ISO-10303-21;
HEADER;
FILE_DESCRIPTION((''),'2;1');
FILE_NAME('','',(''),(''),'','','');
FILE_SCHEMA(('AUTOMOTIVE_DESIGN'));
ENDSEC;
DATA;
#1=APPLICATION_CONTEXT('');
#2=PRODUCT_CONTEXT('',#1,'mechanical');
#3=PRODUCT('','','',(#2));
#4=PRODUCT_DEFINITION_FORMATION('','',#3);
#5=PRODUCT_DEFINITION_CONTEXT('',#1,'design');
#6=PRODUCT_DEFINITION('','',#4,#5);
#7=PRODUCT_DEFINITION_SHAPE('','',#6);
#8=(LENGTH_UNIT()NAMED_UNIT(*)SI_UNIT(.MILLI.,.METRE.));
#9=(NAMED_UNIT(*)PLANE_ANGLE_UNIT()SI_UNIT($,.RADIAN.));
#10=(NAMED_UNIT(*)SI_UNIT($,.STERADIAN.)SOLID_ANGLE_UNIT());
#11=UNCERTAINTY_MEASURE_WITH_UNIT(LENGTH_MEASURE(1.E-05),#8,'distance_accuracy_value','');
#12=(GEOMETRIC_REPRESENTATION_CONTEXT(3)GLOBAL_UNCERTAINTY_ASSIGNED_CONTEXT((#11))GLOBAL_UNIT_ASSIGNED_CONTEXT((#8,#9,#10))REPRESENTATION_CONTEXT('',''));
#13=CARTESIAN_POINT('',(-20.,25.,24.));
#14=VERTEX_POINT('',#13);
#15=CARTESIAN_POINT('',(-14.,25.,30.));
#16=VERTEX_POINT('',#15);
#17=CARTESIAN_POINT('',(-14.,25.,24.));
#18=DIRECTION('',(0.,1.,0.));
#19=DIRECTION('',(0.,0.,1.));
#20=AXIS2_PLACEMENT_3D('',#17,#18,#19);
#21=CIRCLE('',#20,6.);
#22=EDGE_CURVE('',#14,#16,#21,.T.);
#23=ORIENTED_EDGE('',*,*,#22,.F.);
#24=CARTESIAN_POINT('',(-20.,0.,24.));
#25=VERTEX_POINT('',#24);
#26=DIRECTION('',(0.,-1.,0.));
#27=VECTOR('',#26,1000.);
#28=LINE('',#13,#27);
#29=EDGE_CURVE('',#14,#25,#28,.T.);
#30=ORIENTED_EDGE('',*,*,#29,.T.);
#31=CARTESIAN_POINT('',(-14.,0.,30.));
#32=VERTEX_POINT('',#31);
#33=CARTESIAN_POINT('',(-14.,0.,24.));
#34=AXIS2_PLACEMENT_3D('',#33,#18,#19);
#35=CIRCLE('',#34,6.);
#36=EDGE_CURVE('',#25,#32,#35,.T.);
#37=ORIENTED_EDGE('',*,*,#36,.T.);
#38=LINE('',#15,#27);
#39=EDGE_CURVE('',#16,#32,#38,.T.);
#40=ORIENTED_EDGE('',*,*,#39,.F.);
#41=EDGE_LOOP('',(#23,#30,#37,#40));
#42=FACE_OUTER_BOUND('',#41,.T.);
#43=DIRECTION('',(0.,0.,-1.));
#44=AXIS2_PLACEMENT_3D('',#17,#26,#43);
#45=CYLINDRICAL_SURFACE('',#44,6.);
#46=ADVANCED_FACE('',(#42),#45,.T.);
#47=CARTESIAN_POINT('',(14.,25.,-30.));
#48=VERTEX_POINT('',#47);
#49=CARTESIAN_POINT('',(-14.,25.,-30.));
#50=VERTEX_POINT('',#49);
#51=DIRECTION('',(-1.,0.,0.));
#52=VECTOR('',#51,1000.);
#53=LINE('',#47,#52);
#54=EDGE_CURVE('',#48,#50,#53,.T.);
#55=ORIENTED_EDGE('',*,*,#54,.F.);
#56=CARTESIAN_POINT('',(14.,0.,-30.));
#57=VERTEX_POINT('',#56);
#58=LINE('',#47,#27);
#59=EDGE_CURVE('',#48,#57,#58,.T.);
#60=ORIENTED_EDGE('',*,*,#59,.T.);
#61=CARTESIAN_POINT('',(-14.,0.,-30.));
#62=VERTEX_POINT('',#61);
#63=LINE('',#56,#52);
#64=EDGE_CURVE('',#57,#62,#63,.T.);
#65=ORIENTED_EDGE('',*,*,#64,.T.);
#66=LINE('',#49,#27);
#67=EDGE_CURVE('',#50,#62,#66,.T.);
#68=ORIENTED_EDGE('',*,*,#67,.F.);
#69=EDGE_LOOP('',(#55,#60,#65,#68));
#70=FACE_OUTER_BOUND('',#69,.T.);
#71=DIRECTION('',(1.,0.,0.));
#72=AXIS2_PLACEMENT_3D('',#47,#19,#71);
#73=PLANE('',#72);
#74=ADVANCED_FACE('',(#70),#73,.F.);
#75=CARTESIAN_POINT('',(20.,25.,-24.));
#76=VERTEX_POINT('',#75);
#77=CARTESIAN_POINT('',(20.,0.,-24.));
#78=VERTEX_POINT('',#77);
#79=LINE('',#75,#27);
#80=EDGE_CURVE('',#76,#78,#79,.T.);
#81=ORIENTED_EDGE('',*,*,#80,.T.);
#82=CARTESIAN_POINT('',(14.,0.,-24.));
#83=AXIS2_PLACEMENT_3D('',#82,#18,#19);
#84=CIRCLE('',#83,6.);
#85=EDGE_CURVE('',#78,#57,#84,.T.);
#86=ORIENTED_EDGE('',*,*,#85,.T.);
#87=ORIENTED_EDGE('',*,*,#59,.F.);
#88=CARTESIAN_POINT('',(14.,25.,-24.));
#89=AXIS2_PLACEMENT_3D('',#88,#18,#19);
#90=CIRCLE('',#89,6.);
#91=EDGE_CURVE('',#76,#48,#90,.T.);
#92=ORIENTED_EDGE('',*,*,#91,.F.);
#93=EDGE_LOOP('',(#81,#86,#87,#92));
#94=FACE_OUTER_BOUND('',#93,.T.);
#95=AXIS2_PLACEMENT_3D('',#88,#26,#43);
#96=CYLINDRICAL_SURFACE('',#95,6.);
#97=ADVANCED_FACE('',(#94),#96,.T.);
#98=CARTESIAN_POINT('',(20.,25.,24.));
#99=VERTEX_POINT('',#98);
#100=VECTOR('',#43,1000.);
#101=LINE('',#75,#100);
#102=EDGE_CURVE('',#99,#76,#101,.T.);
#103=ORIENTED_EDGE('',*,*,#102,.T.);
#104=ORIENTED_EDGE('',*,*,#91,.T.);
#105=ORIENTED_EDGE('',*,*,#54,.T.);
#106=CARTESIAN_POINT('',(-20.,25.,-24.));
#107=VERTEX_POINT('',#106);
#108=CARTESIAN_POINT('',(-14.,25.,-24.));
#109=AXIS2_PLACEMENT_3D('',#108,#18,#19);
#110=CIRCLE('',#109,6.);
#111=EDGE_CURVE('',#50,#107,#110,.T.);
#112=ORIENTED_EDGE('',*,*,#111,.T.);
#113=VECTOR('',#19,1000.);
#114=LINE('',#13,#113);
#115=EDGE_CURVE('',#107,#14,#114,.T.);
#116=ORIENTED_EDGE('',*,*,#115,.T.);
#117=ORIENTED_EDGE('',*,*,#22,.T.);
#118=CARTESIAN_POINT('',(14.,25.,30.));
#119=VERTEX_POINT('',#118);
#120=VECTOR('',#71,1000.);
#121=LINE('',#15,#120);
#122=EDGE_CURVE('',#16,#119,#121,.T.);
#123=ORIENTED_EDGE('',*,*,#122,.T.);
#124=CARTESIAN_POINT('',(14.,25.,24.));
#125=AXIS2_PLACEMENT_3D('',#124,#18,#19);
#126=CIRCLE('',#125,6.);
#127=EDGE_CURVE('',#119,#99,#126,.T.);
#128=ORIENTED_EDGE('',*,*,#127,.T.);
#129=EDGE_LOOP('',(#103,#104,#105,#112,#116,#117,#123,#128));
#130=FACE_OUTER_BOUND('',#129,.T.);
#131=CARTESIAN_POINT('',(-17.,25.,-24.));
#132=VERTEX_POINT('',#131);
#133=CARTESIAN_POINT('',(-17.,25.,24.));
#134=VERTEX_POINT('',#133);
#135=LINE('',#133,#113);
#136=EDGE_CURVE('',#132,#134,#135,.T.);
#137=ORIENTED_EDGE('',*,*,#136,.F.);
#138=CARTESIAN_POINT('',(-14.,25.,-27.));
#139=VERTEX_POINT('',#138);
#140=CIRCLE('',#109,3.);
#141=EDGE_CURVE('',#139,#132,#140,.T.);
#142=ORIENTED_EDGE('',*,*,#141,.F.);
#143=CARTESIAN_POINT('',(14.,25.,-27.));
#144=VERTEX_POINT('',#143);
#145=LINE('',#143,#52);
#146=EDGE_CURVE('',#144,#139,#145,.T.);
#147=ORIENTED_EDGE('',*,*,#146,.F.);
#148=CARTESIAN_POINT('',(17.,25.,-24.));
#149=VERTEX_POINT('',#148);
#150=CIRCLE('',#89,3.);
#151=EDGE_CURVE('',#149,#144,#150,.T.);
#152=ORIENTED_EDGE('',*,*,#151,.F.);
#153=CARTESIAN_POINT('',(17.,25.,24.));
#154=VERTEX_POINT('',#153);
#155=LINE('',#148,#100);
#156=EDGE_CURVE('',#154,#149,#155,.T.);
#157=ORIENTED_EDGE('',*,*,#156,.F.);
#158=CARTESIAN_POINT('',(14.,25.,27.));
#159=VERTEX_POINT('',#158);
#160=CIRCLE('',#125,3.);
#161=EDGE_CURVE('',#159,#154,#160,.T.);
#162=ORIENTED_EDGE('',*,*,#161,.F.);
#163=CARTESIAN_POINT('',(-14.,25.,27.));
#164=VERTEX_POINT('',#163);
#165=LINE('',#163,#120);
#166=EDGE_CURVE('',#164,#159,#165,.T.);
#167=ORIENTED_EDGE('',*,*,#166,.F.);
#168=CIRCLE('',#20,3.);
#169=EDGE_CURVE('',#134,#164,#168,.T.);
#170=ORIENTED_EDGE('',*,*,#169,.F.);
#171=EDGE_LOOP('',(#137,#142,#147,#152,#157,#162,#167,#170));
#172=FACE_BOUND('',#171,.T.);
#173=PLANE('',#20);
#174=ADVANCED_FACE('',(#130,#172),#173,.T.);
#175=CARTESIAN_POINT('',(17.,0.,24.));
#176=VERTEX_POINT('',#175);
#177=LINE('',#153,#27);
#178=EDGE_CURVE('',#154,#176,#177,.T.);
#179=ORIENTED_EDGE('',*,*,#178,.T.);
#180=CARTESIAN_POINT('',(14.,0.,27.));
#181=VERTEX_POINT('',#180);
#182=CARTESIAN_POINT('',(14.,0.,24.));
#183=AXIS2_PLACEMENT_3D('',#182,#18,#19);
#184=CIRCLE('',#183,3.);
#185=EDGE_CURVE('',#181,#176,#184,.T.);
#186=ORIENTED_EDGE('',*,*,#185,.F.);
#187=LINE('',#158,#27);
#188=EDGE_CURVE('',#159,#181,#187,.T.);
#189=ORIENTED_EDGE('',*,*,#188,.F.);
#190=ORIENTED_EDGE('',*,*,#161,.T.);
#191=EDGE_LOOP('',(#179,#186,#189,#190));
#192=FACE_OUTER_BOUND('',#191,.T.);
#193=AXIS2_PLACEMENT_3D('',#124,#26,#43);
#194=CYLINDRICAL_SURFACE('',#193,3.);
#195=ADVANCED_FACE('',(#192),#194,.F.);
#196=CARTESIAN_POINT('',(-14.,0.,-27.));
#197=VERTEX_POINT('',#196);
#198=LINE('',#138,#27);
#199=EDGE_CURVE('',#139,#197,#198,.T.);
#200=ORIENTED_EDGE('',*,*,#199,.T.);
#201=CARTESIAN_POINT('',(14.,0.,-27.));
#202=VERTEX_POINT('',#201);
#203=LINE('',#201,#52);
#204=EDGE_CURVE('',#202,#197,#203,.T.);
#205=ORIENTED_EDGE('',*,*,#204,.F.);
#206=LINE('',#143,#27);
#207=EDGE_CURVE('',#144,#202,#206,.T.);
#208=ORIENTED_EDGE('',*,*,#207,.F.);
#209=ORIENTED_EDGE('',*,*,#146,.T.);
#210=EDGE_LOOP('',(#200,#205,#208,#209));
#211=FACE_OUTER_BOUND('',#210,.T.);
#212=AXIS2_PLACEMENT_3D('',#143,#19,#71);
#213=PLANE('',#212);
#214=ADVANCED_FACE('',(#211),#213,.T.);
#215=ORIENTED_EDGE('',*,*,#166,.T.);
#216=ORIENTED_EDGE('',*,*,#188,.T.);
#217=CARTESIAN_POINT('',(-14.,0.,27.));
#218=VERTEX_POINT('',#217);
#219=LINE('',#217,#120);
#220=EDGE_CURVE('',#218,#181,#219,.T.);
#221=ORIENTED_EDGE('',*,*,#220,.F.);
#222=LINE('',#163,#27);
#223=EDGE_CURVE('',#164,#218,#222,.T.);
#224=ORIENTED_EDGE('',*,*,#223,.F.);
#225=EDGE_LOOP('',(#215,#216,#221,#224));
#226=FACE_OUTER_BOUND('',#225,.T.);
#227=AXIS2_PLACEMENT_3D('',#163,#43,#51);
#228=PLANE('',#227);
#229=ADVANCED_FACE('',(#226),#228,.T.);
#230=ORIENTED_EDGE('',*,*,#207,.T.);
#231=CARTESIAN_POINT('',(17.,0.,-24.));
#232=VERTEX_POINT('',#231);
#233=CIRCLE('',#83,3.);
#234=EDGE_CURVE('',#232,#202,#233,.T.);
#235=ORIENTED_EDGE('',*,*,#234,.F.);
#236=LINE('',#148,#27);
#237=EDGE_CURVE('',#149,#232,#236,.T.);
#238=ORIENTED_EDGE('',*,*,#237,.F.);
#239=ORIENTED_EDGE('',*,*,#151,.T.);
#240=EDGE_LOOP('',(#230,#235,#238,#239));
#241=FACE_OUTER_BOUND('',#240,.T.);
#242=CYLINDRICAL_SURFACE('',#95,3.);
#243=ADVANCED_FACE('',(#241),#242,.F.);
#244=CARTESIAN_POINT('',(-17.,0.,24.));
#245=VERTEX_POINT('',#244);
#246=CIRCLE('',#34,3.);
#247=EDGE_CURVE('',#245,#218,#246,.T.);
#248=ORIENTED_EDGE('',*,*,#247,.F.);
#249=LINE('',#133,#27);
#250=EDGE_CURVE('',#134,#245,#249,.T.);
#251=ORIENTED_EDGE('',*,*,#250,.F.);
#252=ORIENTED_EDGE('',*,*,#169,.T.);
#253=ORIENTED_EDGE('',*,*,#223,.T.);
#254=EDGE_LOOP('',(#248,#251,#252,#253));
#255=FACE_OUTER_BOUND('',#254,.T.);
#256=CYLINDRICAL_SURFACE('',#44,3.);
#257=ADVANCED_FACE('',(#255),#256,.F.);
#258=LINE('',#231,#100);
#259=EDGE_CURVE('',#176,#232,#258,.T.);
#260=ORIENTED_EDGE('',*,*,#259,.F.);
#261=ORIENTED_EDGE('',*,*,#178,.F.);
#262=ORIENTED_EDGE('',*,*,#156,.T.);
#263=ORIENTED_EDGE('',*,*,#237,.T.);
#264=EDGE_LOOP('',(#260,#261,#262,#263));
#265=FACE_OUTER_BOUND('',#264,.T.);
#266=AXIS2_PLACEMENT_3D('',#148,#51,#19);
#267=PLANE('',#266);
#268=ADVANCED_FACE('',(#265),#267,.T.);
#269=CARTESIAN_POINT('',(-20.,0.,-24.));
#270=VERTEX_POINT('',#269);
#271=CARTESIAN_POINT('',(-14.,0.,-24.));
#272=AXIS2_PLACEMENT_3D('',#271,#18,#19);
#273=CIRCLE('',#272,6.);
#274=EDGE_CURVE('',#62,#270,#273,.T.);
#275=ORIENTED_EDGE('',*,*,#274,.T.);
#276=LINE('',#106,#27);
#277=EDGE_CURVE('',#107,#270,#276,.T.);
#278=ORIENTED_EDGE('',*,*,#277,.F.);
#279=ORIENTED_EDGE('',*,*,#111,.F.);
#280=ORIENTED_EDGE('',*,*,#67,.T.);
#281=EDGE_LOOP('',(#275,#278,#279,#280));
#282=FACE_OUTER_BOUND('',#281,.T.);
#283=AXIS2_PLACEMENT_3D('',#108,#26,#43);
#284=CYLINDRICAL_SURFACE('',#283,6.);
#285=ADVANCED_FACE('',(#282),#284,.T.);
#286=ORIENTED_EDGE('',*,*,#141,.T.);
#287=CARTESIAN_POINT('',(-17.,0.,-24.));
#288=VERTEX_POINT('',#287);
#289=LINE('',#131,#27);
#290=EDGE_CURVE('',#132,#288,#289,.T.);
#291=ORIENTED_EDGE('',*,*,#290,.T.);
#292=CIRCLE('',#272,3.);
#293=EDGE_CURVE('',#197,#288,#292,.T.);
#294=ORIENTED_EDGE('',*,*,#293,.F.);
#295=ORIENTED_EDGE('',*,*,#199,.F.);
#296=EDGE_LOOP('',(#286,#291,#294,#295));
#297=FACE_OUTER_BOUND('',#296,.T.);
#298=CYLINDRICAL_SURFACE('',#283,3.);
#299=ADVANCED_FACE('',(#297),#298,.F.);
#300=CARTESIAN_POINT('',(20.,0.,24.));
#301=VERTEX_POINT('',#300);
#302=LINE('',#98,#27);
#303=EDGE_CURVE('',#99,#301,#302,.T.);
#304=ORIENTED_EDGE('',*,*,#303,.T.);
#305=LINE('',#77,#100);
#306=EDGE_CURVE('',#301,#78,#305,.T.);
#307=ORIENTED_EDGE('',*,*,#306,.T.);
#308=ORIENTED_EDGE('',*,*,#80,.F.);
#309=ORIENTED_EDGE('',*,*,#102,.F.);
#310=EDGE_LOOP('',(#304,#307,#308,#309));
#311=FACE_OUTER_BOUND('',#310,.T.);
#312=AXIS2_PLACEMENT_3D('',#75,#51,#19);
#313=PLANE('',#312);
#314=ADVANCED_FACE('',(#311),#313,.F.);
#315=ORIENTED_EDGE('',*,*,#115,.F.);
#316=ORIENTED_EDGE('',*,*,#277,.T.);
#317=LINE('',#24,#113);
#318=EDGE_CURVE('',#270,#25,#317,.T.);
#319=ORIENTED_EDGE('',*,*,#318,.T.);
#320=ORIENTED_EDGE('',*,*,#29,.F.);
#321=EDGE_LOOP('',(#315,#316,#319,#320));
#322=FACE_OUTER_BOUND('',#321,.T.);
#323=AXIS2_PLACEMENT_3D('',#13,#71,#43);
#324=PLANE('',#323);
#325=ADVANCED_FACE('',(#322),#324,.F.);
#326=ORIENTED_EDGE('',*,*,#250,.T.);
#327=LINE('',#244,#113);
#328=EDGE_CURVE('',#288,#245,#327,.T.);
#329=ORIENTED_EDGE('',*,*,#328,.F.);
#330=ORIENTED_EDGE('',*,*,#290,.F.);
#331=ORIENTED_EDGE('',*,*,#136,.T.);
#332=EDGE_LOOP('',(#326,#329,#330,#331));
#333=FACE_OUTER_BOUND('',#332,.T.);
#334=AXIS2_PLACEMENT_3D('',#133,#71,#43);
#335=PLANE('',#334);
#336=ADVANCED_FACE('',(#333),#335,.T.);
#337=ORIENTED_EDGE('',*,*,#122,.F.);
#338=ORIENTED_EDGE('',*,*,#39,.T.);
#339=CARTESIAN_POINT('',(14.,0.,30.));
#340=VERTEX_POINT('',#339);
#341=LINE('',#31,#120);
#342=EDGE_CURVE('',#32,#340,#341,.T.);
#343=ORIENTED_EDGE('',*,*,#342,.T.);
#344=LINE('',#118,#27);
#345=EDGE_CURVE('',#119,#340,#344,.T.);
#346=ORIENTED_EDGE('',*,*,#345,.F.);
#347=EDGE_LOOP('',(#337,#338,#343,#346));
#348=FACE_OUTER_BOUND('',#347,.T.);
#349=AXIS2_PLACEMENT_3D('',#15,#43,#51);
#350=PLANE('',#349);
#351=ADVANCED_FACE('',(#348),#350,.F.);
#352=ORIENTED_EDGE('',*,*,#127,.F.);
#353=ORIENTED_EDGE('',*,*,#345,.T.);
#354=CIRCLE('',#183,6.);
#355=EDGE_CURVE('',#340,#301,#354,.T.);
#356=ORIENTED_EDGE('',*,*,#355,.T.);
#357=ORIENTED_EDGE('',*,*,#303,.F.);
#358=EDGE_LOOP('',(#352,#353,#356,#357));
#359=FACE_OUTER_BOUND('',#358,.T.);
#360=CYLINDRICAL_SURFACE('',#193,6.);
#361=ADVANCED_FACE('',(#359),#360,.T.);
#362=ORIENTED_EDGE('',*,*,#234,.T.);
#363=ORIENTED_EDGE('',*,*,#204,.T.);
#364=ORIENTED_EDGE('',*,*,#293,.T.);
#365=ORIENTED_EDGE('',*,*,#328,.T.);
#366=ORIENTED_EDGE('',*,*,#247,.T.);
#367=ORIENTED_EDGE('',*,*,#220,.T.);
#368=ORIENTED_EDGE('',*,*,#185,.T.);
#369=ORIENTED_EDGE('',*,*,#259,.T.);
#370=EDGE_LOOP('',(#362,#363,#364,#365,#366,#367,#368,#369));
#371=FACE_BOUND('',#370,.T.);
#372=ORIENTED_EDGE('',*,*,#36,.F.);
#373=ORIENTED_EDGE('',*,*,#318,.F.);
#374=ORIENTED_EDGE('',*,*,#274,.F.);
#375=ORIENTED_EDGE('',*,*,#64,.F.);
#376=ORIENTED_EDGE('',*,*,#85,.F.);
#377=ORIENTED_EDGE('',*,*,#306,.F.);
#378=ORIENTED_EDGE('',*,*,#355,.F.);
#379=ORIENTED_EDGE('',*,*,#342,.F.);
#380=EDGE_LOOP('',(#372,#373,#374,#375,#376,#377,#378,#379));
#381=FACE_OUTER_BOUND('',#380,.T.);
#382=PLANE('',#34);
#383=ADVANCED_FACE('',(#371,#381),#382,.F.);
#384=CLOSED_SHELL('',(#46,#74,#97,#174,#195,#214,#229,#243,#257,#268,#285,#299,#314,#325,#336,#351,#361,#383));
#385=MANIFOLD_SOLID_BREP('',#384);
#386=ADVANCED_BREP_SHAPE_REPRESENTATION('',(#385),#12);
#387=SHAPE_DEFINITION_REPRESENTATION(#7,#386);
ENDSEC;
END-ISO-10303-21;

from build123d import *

# Parameters (mm, degrees)
GB_T_6728_2002_RECTANGULAR_HOLLOW_SECTIO_DEPTH = 25


with BuildPart() as part:
    # Sketch13 → GB/T 6728-2002 Rectangular Hollow Section 60X40X3(1) (new body)
    with BuildSketch(Plane(origin=(0, 0, 0), x_dir=(-1, 0, 0), z_dir=(0, 1, 0))):
        with BuildLine():
            Line((-14, -30), (14, -30))
            ThreePointArc((14, -30), (18.242640687, -28.242640687), (20, -24))
            Line((20, -24), (20, 24))
            ThreePointArc((20, 24), (18.242640687, 28.242640687), (14, 30))
            Line((14, 30), (-14, 30))
            ThreePointArc((-14, 30), (-18.242640687, 28.242640687), (-20, 24))
            Line((-20, 24), (-20, -24))
            ThreePointArc((-20, -24), (-18.242640687, -28.242640687), (-14, -30))
        make_face()
        with BuildLine():
            Line((-14, -27), (14, -27))
            ThreePointArc((14, -27), (16.121320344, -26.121320344), (17, -24))
            Line((17, -24), (17, 24))
            ThreePointArc((17, 24), (16.121320344, 26.121320344), (14, 27))
            Line((14, 27), (-14, 27))
            ThreePointArc((-14, 27), (-16.121320344, 26.121320344), (-17, 24))
            Line((-17, 24), (-17, -24))
            ThreePointArc((-17, -24), (-16.121320344, -26.121320344), (-14, -27))
        make_face(mode=Mode.SUBTRACT)
    extrude(amount=GB_T_6728_2002_RECTANGULAR_HOLLOW_SECTIO_DEPTH)


solid = part.part
